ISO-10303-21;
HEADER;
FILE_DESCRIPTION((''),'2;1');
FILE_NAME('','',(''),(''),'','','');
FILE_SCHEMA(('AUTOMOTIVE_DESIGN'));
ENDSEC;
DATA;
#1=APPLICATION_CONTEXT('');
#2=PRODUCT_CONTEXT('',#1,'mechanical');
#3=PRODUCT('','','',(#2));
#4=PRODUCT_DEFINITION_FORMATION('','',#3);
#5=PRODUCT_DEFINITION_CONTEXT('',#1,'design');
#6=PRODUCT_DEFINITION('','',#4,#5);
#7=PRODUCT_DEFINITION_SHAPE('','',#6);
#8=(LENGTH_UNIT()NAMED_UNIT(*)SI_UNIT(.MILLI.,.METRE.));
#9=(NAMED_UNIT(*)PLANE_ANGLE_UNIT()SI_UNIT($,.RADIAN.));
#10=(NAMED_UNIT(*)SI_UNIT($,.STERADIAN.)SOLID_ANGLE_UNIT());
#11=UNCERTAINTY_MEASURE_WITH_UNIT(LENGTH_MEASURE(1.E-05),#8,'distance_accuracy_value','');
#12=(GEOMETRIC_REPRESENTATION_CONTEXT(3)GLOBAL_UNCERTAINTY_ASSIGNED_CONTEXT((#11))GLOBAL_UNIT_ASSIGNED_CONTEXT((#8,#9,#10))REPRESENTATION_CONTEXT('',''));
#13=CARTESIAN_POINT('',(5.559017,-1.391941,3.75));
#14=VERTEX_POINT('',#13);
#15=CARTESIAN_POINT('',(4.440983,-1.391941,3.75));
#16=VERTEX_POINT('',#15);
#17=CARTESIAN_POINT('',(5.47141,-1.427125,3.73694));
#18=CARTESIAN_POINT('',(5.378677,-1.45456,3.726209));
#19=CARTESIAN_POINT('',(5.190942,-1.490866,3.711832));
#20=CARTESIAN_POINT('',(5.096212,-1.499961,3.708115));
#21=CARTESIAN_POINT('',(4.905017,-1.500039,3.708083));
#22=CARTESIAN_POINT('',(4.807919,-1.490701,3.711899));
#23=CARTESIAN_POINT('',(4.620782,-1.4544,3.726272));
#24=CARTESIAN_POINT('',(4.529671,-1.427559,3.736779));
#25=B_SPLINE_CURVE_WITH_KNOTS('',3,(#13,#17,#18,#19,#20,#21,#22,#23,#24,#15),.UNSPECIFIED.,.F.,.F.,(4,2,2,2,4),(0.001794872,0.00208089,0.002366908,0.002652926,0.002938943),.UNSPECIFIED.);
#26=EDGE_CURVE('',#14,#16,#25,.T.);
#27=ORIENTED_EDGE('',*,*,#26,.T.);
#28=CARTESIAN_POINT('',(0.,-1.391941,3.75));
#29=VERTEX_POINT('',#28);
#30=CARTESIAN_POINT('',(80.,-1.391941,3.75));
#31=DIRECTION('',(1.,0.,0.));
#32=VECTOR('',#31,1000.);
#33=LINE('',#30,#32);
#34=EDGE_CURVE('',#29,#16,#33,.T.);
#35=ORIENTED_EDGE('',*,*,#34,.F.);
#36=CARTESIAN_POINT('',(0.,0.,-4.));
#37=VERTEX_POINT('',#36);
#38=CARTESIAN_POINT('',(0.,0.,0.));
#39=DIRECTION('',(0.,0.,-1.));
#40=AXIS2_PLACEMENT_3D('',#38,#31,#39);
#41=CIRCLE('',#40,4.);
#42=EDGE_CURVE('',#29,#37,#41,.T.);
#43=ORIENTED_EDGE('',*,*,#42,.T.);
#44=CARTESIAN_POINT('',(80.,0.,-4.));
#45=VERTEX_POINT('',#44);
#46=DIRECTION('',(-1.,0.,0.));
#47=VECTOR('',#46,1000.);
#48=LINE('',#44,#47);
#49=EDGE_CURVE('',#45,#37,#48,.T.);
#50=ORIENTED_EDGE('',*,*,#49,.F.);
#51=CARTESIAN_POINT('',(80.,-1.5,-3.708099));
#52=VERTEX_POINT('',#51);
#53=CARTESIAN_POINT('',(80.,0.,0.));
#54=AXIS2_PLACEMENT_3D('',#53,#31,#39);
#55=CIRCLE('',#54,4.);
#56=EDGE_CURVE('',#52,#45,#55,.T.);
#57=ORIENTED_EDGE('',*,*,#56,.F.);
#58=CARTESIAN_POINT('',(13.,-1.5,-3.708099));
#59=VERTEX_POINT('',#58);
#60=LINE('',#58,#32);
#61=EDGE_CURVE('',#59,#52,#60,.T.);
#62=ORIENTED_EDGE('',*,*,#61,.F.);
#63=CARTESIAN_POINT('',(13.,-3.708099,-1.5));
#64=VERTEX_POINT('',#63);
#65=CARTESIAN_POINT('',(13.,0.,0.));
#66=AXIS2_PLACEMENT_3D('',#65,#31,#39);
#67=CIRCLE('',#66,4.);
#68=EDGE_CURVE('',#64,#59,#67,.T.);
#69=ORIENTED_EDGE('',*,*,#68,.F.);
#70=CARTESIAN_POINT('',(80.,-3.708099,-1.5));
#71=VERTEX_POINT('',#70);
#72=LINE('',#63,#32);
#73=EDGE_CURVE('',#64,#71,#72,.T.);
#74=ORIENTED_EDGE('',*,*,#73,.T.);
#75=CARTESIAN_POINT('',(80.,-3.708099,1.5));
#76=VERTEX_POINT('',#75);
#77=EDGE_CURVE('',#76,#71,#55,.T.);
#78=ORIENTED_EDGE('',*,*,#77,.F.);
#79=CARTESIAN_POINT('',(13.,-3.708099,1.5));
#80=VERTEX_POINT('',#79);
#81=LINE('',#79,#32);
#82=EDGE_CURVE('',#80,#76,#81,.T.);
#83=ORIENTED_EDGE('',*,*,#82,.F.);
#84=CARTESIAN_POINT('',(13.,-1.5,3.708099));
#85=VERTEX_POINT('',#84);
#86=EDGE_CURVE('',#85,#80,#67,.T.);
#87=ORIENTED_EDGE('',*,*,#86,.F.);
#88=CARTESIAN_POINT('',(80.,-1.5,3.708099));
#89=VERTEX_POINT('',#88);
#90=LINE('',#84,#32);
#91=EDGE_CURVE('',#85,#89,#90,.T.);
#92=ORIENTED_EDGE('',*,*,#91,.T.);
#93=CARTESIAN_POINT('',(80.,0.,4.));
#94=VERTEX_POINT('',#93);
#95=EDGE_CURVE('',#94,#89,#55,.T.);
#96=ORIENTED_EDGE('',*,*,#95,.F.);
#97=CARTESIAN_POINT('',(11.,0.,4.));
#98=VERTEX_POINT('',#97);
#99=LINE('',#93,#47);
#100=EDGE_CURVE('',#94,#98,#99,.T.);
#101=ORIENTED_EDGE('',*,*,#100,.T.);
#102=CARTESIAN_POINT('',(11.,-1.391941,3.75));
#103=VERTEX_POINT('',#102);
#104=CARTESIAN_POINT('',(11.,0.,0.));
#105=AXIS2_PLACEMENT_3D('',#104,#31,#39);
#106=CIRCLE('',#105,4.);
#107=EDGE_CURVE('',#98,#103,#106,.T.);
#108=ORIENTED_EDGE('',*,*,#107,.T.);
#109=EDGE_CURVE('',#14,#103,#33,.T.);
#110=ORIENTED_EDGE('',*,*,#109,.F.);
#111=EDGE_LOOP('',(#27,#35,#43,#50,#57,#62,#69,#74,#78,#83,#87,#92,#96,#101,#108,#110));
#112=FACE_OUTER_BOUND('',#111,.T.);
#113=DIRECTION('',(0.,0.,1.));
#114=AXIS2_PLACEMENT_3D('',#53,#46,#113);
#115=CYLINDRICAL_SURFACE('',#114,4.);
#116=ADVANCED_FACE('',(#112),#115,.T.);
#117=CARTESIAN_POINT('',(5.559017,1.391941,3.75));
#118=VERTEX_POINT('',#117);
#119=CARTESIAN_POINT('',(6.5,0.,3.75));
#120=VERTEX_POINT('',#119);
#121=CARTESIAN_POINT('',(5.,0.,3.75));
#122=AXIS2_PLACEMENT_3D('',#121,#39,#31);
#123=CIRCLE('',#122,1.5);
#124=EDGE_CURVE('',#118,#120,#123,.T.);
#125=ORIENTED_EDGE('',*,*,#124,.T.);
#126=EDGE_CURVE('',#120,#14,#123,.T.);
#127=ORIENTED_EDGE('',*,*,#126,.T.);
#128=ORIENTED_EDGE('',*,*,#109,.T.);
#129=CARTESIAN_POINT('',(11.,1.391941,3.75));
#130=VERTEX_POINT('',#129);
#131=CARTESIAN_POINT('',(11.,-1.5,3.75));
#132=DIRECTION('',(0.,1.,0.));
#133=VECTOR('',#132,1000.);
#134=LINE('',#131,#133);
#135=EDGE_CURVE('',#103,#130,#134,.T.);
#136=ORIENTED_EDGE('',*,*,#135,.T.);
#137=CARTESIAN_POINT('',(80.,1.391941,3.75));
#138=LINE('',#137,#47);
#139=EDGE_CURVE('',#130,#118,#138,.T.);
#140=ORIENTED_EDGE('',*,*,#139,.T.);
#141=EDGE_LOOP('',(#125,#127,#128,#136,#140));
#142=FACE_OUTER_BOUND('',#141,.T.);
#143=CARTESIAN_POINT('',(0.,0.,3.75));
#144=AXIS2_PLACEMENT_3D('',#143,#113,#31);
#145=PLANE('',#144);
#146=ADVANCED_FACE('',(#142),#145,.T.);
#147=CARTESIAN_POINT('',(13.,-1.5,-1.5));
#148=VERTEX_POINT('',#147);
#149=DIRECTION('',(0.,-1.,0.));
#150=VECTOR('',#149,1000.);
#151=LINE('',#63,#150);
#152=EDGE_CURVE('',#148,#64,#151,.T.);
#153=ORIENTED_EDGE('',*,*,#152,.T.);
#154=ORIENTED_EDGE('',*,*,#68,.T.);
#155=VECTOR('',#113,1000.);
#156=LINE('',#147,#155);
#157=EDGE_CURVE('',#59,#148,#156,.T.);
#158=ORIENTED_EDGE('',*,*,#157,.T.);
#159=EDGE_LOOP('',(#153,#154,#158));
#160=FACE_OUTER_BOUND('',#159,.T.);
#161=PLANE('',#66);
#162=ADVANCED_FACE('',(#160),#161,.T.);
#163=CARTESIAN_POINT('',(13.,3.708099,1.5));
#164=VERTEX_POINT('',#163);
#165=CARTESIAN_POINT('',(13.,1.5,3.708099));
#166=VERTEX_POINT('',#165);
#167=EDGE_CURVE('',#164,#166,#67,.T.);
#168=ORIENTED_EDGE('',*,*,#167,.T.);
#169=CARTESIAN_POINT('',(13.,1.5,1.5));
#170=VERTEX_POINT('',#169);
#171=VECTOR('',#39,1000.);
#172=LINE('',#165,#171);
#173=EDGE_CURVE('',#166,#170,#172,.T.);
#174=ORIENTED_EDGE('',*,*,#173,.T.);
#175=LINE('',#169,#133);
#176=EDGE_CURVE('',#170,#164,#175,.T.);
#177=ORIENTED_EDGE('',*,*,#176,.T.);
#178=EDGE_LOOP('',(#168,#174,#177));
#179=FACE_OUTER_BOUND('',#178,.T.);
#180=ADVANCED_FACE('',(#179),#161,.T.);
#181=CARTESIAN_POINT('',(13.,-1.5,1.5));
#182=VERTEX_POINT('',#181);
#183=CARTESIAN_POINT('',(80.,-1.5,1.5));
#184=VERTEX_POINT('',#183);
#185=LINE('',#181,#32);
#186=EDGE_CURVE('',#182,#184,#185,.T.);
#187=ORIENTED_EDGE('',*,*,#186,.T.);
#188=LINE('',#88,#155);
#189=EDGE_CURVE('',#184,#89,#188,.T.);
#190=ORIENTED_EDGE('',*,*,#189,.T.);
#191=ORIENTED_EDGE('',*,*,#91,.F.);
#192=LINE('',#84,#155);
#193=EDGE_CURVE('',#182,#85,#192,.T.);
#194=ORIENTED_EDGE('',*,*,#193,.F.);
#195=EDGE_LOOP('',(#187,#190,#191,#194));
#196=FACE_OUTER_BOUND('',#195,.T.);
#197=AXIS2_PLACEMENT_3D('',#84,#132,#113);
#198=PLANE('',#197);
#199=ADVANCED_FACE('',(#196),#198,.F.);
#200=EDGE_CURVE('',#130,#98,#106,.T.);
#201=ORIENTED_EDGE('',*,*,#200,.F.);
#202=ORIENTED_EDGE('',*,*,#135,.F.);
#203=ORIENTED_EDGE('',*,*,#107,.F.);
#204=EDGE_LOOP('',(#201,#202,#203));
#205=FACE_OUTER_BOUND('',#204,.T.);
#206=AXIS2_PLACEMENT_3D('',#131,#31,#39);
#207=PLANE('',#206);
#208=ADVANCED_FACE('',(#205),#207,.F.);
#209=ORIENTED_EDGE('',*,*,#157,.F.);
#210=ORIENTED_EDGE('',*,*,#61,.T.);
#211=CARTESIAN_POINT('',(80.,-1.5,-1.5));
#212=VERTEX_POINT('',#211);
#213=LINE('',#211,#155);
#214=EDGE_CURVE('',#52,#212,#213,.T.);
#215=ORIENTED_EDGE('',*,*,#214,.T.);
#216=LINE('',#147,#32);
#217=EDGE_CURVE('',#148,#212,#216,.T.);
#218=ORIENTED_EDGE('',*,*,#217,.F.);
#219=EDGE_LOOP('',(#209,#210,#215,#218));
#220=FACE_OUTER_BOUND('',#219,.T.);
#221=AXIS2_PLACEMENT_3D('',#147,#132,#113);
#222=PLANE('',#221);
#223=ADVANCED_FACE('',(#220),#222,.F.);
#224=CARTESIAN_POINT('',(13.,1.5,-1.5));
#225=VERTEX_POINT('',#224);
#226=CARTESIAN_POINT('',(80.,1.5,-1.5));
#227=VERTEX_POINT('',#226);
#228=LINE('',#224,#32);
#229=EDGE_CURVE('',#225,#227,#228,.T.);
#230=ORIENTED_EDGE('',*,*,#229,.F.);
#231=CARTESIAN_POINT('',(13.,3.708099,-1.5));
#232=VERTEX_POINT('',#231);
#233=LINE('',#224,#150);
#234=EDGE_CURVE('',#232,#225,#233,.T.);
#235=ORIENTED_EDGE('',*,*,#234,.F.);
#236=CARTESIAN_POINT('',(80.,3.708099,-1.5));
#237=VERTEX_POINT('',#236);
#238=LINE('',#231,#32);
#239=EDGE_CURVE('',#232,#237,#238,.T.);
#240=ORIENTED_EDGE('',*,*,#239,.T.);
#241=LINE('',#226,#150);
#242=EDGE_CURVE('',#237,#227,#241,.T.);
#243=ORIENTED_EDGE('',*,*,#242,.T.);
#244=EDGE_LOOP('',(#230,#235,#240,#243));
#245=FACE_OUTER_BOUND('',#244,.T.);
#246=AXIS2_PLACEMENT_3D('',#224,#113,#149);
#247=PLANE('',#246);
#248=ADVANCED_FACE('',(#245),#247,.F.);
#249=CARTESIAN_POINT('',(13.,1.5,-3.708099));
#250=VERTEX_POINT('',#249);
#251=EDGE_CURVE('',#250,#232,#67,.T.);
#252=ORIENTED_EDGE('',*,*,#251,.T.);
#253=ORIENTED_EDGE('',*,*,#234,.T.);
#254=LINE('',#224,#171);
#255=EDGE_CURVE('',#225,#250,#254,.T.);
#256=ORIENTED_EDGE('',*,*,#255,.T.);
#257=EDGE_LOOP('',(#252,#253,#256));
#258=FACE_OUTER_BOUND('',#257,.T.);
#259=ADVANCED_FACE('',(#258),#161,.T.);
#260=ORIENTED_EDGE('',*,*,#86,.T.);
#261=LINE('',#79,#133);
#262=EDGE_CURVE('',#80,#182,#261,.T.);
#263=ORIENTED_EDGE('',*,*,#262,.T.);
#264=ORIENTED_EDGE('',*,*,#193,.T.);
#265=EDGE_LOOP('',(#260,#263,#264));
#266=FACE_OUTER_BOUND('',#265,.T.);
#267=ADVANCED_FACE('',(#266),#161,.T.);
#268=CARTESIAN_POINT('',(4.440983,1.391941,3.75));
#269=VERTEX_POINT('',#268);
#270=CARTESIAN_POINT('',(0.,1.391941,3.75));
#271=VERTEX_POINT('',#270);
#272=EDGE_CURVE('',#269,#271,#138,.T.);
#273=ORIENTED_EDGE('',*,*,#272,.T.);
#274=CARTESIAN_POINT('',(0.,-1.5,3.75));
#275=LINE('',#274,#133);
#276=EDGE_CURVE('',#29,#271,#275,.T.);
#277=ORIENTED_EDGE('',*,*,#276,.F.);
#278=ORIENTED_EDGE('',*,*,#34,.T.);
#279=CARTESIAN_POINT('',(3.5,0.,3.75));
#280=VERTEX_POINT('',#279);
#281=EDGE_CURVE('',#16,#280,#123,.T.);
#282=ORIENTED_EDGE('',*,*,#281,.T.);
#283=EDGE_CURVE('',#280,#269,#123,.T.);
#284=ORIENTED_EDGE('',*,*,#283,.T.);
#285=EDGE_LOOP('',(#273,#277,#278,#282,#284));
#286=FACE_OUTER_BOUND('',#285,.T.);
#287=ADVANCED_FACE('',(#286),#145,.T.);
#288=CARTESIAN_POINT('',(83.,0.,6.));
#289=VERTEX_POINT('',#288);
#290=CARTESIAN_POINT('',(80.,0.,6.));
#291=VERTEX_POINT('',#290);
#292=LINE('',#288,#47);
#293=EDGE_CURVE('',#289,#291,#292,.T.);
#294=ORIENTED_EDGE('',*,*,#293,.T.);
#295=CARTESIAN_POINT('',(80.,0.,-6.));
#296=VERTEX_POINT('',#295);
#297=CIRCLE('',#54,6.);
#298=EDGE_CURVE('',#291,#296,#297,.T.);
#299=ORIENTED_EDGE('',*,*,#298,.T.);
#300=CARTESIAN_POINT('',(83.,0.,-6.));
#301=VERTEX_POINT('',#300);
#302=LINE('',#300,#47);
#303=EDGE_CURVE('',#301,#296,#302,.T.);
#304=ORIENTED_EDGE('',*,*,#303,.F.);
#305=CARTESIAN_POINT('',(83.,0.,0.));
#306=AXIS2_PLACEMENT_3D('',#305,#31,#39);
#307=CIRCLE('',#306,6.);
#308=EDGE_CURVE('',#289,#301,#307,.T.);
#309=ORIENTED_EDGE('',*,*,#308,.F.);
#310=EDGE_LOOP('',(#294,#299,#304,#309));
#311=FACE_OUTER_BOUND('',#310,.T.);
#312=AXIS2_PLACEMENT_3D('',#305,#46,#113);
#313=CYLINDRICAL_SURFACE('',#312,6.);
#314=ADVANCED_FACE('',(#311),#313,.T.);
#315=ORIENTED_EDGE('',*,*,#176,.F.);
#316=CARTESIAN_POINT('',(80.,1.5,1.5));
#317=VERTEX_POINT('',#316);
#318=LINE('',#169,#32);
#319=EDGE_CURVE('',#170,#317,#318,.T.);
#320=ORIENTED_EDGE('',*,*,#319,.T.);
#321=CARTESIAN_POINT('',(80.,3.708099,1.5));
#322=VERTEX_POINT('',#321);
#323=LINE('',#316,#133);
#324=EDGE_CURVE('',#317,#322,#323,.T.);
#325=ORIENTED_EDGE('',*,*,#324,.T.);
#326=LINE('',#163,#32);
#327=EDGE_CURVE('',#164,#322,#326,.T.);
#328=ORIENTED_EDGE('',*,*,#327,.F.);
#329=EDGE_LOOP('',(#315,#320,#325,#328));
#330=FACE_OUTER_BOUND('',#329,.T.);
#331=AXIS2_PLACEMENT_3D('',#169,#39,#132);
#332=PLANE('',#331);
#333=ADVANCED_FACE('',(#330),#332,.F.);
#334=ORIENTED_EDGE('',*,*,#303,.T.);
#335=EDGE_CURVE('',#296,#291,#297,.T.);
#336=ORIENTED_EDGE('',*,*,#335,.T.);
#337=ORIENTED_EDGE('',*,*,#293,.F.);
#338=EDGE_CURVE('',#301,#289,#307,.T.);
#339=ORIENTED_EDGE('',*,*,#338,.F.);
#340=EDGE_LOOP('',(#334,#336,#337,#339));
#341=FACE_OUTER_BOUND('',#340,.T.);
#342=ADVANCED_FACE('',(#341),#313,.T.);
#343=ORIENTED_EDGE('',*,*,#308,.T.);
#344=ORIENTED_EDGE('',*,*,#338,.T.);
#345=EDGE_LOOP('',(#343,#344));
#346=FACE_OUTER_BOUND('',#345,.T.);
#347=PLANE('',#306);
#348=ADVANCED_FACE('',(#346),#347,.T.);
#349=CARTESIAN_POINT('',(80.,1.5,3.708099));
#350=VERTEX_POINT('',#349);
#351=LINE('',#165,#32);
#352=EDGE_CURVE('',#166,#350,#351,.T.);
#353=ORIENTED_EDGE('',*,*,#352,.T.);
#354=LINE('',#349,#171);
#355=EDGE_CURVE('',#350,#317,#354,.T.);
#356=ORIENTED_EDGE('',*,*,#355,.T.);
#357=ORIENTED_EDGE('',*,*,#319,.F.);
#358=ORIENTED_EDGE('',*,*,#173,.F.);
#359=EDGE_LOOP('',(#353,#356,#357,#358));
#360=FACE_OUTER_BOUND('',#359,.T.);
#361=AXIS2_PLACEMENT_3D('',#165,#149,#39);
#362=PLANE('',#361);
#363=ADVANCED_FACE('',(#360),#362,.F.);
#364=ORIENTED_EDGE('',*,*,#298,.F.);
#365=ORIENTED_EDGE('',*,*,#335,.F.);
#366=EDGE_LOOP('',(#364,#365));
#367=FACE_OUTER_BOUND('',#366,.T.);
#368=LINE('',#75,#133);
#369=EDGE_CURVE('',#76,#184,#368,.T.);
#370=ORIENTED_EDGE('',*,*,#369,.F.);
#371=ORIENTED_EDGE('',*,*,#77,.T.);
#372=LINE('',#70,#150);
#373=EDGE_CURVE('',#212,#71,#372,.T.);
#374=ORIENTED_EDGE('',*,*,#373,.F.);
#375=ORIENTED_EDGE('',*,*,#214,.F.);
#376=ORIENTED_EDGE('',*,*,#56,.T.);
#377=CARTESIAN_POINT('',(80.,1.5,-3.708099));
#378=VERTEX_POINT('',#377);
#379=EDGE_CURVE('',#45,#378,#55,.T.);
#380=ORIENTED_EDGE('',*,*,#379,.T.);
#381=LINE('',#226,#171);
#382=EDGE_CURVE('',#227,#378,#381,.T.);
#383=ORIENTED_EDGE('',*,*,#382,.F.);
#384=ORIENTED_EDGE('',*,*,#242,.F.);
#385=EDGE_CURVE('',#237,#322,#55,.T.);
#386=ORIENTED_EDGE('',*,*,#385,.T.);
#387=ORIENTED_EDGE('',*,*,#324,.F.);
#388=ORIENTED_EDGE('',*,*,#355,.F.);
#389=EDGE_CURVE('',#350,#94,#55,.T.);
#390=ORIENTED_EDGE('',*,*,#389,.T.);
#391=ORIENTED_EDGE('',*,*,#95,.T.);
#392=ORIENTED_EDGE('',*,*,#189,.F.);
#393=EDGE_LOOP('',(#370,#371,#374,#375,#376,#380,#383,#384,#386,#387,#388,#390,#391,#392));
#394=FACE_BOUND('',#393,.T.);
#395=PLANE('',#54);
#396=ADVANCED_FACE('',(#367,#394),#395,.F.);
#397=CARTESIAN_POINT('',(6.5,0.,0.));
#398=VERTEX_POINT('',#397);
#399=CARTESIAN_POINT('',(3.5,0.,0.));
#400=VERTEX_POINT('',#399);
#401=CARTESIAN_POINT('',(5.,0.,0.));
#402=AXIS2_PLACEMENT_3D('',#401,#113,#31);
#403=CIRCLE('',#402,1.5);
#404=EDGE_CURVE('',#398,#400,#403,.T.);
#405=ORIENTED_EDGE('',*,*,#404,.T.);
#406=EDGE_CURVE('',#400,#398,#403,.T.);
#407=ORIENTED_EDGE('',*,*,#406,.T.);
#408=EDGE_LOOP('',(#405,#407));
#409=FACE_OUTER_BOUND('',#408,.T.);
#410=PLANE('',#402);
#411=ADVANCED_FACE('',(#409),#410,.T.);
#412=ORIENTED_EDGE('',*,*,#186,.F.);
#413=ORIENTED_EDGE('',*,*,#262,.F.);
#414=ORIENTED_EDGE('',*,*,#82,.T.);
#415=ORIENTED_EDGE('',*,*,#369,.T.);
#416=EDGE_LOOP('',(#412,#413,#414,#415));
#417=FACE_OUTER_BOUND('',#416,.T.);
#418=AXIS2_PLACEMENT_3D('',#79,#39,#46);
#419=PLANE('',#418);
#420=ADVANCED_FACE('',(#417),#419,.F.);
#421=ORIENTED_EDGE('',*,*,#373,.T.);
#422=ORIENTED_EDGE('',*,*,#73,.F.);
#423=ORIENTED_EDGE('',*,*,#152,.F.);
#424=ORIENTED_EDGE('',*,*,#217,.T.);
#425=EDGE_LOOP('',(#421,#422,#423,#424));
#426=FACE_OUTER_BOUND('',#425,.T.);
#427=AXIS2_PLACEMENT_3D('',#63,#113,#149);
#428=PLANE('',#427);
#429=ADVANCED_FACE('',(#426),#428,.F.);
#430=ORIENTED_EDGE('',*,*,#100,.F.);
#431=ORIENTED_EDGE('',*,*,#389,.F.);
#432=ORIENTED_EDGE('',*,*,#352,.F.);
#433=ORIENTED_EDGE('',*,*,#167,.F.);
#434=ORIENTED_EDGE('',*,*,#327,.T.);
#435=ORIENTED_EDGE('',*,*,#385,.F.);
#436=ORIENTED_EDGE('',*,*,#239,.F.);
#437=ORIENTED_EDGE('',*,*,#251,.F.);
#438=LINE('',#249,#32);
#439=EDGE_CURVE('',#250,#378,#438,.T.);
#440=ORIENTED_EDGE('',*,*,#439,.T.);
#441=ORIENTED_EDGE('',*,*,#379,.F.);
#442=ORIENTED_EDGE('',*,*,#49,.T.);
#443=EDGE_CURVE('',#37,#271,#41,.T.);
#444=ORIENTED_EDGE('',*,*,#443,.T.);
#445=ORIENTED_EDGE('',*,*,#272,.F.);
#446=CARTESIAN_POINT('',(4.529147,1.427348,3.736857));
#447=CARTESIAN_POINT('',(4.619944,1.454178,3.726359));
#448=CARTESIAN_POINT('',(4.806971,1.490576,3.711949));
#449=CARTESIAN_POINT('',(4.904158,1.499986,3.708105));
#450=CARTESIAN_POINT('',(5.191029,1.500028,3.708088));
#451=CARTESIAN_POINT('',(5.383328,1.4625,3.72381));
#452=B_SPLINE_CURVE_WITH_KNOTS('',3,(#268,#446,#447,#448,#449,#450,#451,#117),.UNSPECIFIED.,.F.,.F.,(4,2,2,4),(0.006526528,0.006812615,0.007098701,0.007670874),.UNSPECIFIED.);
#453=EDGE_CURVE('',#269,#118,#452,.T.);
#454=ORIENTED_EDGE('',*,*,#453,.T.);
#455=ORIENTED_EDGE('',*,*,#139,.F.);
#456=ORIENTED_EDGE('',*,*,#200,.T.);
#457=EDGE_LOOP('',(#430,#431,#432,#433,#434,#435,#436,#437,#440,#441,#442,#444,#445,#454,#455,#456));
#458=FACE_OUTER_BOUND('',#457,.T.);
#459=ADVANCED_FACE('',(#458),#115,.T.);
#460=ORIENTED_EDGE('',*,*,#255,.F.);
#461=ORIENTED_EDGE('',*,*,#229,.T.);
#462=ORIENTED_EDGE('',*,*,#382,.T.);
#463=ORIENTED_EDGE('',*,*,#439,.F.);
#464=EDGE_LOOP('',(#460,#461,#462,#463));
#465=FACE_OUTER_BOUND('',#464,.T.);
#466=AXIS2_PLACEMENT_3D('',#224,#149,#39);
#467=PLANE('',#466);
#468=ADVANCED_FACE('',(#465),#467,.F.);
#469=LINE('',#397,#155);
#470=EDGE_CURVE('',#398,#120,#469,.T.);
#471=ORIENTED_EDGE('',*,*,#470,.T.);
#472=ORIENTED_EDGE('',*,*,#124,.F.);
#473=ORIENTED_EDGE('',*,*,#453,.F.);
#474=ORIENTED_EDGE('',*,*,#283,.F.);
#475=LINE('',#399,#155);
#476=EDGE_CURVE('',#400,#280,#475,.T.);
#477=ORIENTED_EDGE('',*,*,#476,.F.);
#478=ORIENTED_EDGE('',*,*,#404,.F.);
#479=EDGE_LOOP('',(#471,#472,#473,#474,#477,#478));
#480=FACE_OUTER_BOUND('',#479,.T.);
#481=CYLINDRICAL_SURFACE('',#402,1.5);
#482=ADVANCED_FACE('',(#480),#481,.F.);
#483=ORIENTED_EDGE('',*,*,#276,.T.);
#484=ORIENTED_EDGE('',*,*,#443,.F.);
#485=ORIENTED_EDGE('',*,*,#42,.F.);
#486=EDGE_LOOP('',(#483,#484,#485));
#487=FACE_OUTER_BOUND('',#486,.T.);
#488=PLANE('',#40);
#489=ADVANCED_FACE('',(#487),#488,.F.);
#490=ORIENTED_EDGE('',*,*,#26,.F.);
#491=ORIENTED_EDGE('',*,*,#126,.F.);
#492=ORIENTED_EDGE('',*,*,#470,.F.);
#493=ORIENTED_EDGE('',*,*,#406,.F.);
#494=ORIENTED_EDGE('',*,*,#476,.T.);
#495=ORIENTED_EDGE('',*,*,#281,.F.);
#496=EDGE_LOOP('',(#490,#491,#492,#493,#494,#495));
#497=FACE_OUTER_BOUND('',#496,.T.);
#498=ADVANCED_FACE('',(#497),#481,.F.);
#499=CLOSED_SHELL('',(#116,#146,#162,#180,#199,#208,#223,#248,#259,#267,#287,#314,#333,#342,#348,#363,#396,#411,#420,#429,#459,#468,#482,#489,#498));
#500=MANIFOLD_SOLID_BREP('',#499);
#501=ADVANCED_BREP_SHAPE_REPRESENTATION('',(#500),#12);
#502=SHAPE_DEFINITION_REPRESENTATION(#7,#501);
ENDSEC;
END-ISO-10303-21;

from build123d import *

# Parameters (mm, degrees)
SHANK_PROFILE_8_R           = 4
SHANK_8X80_DEPTH            = 80
SHANK_START                 = -67
SHANK_FLATS_67MM_DEPTH      = 67
HEAD_PROFILE_12_R           = 6
HEAD_12X3_DEPTH             = 3
END_CUT_PROFILE_R           = 1.5
END_POCKET_CUT_4MM_DEPTH    = 4
SKETCH5_4_W                 = 11
SKETCH5_4_H                 = 3
END_RELIEF_CUT_0_25MM_DEPTH = 0.25


with BuildPart() as part:
    # Shank Profile _8 → Shank _8x80 (new body)
    with BuildSketch(Plane(origin=(0, 0, 0), x_dir=(0, 0, -1), z_dir=(1, 0, 0))):
        Circle(SHANK_PROFILE_8_R)
    extrude(amount=SHANK_8X80_DEPTH)

    # Shank Flats Profile → Shank Flats 67mm (cut)
    with BuildSketch(Plane(origin=(80, 0, 0), x_dir=(0, 0, -1), z_dir=(1, 0, 0)).offset(SHANK_START)):
        with BuildLine():
            Line((-1.5, 1.5), (-1.5, 3.708099244))
            ThreePointArc((-1.5, 3.708099244), (-2.828427125, 2.828427125), (-3.708099244, 1.5))
            Line((-3.708099244, 1.5), (-1.5, 1.5))
        make_face()
        with BuildLine():
            Line((1.5, 1.5), (1.5, 3.708099244))
            ThreePointArc((1.5, 3.708099244), (2.828427125, 2.828427125), (3.708099244, 1.5))
            Line((3.708099244, 1.5), (1.5, 1.5))
        make_face()
        with BuildLine():
            Line((1.5, -3.708099244), (1.5, -1.5))
            Line((1.5, -1.5), (3.708099244, -1.5))
            ThreePointArc((3.708099244, -1.5), (2.828427125, -2.828427125), (1.5, -3.708099244))
        make_face()
        with BuildLine():
            Line((-3.708099244, -1.5), (-1.5, -1.5))
            Line((-1.5, -1.5), (-1.5, -3.708099244))
            ThreePointArc((-1.5, -3.708099244), (-2.828427125, -2.828427125), (-3.708099244, -1.5))
        make_face()
    extrude(amount=SHANK_FLATS_67MM_DEPTH, mode=Mode.SUBTRACT)

    # Head Profile _12 → Head _12x3 (add)
    with BuildSketch(Plane(origin=(80, 0, 0), x_dir=(0, 0, -1), z_dir=(1, 0, 0))):
        Circle(HEAD_PROFILE_12_R)
    extrude(amount=HEAD_12X3_DEPTH)

    # End Cut Profile → End Pocket Cut 4mm (cut)
    with BuildSketch(Plane.XY.offset(4)):
        with Locations((5, 0)):
            Circle(END_CUT_PROFILE_R)
    extrude(amount=-END_POCKET_CUT_4MM_DEPTH, mode=Mode.SUBTRACT)

    # Sketch5_4 → End Relief Cut 0.25mm (cut)
    with BuildSketch(Plane.XY.offset(4)):
        with Locations((5.5, 0)):
            Rectangle(SKETCH5_4_W, SKETCH5_4_H)
    extrude(amount=-END_RELIEF_CUT_0_25MM_DEPTH, mode=Mode.SUBTRACT)


solid = part.part
